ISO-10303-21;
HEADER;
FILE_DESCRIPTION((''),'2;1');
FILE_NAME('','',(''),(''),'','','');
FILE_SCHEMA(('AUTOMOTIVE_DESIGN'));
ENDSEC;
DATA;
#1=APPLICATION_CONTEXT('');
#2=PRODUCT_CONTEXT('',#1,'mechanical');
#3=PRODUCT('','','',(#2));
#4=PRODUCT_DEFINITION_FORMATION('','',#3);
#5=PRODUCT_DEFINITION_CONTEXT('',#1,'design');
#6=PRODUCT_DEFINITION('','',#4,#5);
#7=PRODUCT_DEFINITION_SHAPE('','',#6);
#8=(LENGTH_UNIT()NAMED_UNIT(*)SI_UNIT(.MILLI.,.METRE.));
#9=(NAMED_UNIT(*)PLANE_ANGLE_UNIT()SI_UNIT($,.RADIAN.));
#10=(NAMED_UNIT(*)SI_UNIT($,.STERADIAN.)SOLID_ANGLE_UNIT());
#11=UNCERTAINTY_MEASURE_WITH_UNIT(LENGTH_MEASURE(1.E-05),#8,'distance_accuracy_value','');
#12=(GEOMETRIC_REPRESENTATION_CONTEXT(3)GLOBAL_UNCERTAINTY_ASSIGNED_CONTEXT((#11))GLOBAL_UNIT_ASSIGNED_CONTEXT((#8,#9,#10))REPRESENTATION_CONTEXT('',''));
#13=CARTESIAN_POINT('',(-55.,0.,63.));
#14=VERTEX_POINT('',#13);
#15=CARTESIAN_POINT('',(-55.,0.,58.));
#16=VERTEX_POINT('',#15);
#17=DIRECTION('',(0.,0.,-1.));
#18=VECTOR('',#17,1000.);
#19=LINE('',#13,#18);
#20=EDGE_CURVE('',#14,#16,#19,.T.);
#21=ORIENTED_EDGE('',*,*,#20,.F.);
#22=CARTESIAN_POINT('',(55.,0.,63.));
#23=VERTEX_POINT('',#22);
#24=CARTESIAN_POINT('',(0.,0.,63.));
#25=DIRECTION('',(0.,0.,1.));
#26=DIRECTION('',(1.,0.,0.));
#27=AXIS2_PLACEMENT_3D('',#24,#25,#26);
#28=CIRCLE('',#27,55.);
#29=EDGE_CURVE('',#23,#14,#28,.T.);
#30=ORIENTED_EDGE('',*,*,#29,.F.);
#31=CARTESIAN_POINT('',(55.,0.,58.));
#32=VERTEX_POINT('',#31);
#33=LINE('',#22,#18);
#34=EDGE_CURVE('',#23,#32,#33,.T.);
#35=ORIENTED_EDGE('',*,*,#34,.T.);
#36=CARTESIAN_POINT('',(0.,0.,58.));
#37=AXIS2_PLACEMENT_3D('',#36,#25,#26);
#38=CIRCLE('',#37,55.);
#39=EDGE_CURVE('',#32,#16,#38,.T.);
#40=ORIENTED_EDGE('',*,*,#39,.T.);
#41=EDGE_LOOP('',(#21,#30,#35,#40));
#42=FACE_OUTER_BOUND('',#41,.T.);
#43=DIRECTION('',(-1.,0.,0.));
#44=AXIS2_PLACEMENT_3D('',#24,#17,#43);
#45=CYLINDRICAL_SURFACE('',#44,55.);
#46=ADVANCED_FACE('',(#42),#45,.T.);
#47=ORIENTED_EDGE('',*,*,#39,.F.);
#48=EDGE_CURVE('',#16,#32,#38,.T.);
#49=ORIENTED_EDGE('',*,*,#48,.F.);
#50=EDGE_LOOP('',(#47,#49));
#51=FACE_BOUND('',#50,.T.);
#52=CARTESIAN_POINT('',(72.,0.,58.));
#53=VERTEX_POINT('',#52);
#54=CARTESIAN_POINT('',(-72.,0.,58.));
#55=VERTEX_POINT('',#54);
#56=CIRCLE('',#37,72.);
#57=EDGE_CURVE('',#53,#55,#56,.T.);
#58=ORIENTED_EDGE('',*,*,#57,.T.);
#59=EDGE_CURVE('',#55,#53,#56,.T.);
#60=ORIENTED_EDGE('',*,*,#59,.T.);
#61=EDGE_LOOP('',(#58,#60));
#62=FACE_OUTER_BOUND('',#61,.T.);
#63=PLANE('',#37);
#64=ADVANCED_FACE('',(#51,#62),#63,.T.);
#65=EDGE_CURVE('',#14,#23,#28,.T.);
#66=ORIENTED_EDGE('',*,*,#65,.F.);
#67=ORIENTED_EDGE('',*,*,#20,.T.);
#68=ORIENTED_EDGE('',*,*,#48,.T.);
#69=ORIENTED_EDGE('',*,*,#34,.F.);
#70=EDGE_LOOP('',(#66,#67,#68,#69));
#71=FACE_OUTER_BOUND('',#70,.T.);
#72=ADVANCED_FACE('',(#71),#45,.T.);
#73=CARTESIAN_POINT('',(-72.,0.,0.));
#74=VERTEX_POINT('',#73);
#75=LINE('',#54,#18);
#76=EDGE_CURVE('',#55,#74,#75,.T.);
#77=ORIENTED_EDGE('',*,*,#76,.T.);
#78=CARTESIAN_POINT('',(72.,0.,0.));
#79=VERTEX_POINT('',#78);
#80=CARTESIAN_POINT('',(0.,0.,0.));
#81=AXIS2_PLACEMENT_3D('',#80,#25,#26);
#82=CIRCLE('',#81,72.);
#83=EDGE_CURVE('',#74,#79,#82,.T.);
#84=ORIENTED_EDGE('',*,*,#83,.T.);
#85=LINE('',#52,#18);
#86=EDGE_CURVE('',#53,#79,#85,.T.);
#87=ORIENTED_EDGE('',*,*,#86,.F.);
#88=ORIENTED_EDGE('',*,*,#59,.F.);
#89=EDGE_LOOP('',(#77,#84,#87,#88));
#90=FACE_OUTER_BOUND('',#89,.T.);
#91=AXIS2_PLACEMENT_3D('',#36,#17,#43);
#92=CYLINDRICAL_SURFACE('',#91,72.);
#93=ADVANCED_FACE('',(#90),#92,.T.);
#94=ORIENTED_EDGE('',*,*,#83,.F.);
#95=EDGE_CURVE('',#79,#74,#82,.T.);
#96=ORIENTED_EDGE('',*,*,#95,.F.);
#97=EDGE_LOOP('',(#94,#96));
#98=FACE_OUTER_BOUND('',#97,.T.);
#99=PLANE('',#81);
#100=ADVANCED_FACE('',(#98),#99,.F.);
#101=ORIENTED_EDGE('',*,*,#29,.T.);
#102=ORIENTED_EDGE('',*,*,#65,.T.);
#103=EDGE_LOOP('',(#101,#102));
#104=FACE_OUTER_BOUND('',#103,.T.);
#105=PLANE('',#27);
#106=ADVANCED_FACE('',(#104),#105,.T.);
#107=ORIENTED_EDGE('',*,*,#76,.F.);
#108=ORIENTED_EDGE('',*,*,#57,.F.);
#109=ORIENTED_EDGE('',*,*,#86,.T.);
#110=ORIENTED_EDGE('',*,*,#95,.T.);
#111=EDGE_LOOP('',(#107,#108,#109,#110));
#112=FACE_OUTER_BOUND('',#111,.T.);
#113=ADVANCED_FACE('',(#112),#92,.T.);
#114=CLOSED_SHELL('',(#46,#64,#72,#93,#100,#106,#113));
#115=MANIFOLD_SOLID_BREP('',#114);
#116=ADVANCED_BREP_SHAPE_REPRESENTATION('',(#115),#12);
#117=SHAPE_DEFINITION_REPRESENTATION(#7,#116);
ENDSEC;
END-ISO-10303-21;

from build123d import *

# Parameters (mm, degrees)
SKETCH1_R           = 72
BOSS_EXTRUDE1_DEPTH = 58
SKETCH2_R           = 55
BOSS_EXTRUDE2_DEPTH = 5


with BuildPart() as part:
    # Sketch1 → Boss-Extrude1 (new body)
    with BuildSketch(Plane.XY):
        with Locations(Location((0, 0, 0), (0, 0, 180))):
            Circle(SKETCH1_R)
    extrude(amount=BOSS_EXTRUDE1_DEPTH)

    # Sketch2 → Boss-Extrude2 (add)
    with BuildSketch(Plane.XY.offset(58)):
        Circle(SKETCH2_R)
    extrude(amount=BOSS_EXTRUDE2_DEPTH)


solid = part.part
